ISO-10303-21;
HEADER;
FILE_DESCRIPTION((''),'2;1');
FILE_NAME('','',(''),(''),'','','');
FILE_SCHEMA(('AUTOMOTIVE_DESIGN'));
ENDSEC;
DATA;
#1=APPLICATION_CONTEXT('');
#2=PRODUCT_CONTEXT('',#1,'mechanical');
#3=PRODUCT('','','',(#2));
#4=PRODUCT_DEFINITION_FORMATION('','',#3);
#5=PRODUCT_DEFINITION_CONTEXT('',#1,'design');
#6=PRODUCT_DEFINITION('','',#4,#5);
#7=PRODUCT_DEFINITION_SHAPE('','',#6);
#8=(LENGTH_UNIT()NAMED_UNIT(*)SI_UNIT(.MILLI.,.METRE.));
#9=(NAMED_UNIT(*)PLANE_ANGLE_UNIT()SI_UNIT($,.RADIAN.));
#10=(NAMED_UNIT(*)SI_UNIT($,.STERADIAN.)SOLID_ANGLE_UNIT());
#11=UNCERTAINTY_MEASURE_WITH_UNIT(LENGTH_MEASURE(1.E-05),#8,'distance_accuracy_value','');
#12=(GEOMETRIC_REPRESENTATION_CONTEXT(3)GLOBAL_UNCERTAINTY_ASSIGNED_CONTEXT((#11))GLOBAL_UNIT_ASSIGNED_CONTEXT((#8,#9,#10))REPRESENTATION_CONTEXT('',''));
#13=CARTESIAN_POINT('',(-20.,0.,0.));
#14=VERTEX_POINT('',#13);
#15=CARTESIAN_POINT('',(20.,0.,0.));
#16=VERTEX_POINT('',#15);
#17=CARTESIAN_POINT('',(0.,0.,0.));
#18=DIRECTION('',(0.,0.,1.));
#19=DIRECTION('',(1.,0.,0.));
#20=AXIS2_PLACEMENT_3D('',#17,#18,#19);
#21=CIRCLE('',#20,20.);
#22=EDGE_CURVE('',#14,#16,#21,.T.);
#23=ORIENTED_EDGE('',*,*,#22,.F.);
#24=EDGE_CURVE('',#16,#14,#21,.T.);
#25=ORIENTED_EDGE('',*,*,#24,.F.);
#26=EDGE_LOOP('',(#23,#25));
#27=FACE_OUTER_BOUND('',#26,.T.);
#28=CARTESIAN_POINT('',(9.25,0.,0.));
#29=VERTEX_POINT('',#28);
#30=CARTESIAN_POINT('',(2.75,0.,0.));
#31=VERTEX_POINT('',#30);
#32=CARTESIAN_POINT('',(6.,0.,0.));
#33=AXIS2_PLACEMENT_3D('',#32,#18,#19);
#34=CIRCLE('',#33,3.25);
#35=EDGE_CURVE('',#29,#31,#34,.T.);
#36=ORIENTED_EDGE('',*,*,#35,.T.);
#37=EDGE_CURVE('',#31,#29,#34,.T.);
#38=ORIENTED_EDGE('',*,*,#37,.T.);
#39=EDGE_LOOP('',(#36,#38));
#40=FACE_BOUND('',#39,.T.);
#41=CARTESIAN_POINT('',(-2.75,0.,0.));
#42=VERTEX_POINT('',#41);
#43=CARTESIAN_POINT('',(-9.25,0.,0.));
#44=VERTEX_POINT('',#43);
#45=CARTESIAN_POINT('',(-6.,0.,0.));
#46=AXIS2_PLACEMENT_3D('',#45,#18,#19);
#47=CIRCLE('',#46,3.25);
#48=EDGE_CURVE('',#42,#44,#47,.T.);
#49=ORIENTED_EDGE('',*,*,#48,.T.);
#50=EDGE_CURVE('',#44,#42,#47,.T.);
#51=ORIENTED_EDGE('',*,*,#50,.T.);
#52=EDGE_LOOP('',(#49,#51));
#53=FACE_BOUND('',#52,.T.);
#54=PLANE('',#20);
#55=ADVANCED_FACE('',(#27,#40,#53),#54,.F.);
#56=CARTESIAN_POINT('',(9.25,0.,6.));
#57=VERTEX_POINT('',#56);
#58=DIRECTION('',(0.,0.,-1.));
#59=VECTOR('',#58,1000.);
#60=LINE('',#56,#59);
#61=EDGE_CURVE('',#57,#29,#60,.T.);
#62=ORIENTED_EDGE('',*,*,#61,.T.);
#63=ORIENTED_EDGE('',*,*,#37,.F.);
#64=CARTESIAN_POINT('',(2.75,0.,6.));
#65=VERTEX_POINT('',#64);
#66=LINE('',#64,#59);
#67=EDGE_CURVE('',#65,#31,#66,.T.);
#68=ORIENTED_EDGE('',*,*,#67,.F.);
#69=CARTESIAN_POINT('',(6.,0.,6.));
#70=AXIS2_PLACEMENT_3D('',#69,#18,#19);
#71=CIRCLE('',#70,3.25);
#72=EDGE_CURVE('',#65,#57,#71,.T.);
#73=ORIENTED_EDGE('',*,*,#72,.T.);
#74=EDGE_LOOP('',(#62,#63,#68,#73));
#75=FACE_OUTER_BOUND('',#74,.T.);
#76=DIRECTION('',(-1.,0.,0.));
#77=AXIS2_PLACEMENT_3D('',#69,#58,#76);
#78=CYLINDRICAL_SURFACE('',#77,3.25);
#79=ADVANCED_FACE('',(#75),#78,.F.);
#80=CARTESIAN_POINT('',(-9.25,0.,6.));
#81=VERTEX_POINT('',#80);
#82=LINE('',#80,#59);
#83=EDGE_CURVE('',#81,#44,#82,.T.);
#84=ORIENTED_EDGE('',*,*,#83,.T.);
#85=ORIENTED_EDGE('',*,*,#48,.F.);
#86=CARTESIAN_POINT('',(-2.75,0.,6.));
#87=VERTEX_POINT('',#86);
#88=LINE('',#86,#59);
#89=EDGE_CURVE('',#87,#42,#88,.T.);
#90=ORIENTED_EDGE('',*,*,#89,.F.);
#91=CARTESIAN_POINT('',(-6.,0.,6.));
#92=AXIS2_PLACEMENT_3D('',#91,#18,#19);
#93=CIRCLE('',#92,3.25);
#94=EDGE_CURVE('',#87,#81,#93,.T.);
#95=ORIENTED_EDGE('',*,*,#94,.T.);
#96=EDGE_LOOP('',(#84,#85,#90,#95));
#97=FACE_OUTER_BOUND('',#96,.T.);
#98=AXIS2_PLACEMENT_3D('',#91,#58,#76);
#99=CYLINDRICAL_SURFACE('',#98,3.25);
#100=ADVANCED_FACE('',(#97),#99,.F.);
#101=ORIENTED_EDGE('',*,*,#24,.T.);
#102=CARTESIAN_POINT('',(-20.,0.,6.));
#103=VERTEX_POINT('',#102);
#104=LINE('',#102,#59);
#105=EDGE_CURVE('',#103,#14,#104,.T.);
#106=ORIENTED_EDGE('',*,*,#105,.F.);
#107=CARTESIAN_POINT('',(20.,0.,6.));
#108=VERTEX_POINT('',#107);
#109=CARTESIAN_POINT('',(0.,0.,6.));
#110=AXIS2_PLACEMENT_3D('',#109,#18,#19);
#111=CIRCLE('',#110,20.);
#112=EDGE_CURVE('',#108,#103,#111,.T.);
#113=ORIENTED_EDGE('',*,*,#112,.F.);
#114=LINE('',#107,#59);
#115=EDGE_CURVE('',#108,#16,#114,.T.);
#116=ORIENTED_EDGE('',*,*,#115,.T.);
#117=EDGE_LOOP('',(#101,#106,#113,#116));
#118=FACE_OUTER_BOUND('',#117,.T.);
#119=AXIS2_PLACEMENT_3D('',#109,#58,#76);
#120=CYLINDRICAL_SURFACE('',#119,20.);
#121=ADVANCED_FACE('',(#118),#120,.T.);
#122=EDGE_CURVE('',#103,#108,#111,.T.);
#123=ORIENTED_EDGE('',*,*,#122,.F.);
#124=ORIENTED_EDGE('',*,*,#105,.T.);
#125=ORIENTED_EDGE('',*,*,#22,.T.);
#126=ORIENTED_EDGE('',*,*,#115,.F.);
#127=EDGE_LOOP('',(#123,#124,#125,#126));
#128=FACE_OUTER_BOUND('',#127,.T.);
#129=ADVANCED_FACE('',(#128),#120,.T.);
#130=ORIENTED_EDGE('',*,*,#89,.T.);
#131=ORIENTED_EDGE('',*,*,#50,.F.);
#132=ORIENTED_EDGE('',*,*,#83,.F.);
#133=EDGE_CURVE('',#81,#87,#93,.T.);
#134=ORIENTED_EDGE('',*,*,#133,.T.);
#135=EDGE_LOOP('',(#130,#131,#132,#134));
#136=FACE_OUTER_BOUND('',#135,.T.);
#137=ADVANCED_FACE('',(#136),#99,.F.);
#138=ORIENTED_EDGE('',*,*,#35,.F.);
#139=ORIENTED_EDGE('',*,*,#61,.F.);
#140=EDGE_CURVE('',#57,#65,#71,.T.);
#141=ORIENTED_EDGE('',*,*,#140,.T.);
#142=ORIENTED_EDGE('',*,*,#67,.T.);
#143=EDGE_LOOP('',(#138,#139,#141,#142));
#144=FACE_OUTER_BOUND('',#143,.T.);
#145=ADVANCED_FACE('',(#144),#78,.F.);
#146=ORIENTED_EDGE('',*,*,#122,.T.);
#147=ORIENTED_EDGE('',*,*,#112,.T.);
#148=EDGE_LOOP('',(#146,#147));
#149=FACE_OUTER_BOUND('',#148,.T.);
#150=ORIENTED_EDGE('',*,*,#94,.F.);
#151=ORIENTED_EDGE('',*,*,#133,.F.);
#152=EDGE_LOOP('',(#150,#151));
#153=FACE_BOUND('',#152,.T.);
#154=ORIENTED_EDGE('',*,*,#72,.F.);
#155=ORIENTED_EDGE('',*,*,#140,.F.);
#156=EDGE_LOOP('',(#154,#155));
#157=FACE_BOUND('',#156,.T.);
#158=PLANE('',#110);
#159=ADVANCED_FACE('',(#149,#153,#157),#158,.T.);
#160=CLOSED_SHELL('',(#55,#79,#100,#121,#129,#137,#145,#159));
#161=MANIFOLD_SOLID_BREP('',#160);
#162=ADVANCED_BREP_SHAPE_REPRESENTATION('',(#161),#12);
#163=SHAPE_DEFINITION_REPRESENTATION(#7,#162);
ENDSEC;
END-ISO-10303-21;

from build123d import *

# Parameters (mm, degrees)
SKETCH_1_R      = 20
SKETCH_1_R_2    = 3.25
EXTRUDE_1_DEPTH = 6


with BuildPart() as part:
    # 草图1 → 凸台-拉伸1 (new body)
    with BuildSketch(Plane.XY):
        Circle(SKETCH_1_R)
        with Locations((6, 0)):
            Circle(SKETCH_1_R_2, mode=Mode.SUBTRACT)
        with Locations((-6, 0)):
            Circle(SKETCH_1_R_2, mode=Mode.SUBTRACT)
    extrude(amount=EXTRUDE_1_DEPTH)


solid = part.part
